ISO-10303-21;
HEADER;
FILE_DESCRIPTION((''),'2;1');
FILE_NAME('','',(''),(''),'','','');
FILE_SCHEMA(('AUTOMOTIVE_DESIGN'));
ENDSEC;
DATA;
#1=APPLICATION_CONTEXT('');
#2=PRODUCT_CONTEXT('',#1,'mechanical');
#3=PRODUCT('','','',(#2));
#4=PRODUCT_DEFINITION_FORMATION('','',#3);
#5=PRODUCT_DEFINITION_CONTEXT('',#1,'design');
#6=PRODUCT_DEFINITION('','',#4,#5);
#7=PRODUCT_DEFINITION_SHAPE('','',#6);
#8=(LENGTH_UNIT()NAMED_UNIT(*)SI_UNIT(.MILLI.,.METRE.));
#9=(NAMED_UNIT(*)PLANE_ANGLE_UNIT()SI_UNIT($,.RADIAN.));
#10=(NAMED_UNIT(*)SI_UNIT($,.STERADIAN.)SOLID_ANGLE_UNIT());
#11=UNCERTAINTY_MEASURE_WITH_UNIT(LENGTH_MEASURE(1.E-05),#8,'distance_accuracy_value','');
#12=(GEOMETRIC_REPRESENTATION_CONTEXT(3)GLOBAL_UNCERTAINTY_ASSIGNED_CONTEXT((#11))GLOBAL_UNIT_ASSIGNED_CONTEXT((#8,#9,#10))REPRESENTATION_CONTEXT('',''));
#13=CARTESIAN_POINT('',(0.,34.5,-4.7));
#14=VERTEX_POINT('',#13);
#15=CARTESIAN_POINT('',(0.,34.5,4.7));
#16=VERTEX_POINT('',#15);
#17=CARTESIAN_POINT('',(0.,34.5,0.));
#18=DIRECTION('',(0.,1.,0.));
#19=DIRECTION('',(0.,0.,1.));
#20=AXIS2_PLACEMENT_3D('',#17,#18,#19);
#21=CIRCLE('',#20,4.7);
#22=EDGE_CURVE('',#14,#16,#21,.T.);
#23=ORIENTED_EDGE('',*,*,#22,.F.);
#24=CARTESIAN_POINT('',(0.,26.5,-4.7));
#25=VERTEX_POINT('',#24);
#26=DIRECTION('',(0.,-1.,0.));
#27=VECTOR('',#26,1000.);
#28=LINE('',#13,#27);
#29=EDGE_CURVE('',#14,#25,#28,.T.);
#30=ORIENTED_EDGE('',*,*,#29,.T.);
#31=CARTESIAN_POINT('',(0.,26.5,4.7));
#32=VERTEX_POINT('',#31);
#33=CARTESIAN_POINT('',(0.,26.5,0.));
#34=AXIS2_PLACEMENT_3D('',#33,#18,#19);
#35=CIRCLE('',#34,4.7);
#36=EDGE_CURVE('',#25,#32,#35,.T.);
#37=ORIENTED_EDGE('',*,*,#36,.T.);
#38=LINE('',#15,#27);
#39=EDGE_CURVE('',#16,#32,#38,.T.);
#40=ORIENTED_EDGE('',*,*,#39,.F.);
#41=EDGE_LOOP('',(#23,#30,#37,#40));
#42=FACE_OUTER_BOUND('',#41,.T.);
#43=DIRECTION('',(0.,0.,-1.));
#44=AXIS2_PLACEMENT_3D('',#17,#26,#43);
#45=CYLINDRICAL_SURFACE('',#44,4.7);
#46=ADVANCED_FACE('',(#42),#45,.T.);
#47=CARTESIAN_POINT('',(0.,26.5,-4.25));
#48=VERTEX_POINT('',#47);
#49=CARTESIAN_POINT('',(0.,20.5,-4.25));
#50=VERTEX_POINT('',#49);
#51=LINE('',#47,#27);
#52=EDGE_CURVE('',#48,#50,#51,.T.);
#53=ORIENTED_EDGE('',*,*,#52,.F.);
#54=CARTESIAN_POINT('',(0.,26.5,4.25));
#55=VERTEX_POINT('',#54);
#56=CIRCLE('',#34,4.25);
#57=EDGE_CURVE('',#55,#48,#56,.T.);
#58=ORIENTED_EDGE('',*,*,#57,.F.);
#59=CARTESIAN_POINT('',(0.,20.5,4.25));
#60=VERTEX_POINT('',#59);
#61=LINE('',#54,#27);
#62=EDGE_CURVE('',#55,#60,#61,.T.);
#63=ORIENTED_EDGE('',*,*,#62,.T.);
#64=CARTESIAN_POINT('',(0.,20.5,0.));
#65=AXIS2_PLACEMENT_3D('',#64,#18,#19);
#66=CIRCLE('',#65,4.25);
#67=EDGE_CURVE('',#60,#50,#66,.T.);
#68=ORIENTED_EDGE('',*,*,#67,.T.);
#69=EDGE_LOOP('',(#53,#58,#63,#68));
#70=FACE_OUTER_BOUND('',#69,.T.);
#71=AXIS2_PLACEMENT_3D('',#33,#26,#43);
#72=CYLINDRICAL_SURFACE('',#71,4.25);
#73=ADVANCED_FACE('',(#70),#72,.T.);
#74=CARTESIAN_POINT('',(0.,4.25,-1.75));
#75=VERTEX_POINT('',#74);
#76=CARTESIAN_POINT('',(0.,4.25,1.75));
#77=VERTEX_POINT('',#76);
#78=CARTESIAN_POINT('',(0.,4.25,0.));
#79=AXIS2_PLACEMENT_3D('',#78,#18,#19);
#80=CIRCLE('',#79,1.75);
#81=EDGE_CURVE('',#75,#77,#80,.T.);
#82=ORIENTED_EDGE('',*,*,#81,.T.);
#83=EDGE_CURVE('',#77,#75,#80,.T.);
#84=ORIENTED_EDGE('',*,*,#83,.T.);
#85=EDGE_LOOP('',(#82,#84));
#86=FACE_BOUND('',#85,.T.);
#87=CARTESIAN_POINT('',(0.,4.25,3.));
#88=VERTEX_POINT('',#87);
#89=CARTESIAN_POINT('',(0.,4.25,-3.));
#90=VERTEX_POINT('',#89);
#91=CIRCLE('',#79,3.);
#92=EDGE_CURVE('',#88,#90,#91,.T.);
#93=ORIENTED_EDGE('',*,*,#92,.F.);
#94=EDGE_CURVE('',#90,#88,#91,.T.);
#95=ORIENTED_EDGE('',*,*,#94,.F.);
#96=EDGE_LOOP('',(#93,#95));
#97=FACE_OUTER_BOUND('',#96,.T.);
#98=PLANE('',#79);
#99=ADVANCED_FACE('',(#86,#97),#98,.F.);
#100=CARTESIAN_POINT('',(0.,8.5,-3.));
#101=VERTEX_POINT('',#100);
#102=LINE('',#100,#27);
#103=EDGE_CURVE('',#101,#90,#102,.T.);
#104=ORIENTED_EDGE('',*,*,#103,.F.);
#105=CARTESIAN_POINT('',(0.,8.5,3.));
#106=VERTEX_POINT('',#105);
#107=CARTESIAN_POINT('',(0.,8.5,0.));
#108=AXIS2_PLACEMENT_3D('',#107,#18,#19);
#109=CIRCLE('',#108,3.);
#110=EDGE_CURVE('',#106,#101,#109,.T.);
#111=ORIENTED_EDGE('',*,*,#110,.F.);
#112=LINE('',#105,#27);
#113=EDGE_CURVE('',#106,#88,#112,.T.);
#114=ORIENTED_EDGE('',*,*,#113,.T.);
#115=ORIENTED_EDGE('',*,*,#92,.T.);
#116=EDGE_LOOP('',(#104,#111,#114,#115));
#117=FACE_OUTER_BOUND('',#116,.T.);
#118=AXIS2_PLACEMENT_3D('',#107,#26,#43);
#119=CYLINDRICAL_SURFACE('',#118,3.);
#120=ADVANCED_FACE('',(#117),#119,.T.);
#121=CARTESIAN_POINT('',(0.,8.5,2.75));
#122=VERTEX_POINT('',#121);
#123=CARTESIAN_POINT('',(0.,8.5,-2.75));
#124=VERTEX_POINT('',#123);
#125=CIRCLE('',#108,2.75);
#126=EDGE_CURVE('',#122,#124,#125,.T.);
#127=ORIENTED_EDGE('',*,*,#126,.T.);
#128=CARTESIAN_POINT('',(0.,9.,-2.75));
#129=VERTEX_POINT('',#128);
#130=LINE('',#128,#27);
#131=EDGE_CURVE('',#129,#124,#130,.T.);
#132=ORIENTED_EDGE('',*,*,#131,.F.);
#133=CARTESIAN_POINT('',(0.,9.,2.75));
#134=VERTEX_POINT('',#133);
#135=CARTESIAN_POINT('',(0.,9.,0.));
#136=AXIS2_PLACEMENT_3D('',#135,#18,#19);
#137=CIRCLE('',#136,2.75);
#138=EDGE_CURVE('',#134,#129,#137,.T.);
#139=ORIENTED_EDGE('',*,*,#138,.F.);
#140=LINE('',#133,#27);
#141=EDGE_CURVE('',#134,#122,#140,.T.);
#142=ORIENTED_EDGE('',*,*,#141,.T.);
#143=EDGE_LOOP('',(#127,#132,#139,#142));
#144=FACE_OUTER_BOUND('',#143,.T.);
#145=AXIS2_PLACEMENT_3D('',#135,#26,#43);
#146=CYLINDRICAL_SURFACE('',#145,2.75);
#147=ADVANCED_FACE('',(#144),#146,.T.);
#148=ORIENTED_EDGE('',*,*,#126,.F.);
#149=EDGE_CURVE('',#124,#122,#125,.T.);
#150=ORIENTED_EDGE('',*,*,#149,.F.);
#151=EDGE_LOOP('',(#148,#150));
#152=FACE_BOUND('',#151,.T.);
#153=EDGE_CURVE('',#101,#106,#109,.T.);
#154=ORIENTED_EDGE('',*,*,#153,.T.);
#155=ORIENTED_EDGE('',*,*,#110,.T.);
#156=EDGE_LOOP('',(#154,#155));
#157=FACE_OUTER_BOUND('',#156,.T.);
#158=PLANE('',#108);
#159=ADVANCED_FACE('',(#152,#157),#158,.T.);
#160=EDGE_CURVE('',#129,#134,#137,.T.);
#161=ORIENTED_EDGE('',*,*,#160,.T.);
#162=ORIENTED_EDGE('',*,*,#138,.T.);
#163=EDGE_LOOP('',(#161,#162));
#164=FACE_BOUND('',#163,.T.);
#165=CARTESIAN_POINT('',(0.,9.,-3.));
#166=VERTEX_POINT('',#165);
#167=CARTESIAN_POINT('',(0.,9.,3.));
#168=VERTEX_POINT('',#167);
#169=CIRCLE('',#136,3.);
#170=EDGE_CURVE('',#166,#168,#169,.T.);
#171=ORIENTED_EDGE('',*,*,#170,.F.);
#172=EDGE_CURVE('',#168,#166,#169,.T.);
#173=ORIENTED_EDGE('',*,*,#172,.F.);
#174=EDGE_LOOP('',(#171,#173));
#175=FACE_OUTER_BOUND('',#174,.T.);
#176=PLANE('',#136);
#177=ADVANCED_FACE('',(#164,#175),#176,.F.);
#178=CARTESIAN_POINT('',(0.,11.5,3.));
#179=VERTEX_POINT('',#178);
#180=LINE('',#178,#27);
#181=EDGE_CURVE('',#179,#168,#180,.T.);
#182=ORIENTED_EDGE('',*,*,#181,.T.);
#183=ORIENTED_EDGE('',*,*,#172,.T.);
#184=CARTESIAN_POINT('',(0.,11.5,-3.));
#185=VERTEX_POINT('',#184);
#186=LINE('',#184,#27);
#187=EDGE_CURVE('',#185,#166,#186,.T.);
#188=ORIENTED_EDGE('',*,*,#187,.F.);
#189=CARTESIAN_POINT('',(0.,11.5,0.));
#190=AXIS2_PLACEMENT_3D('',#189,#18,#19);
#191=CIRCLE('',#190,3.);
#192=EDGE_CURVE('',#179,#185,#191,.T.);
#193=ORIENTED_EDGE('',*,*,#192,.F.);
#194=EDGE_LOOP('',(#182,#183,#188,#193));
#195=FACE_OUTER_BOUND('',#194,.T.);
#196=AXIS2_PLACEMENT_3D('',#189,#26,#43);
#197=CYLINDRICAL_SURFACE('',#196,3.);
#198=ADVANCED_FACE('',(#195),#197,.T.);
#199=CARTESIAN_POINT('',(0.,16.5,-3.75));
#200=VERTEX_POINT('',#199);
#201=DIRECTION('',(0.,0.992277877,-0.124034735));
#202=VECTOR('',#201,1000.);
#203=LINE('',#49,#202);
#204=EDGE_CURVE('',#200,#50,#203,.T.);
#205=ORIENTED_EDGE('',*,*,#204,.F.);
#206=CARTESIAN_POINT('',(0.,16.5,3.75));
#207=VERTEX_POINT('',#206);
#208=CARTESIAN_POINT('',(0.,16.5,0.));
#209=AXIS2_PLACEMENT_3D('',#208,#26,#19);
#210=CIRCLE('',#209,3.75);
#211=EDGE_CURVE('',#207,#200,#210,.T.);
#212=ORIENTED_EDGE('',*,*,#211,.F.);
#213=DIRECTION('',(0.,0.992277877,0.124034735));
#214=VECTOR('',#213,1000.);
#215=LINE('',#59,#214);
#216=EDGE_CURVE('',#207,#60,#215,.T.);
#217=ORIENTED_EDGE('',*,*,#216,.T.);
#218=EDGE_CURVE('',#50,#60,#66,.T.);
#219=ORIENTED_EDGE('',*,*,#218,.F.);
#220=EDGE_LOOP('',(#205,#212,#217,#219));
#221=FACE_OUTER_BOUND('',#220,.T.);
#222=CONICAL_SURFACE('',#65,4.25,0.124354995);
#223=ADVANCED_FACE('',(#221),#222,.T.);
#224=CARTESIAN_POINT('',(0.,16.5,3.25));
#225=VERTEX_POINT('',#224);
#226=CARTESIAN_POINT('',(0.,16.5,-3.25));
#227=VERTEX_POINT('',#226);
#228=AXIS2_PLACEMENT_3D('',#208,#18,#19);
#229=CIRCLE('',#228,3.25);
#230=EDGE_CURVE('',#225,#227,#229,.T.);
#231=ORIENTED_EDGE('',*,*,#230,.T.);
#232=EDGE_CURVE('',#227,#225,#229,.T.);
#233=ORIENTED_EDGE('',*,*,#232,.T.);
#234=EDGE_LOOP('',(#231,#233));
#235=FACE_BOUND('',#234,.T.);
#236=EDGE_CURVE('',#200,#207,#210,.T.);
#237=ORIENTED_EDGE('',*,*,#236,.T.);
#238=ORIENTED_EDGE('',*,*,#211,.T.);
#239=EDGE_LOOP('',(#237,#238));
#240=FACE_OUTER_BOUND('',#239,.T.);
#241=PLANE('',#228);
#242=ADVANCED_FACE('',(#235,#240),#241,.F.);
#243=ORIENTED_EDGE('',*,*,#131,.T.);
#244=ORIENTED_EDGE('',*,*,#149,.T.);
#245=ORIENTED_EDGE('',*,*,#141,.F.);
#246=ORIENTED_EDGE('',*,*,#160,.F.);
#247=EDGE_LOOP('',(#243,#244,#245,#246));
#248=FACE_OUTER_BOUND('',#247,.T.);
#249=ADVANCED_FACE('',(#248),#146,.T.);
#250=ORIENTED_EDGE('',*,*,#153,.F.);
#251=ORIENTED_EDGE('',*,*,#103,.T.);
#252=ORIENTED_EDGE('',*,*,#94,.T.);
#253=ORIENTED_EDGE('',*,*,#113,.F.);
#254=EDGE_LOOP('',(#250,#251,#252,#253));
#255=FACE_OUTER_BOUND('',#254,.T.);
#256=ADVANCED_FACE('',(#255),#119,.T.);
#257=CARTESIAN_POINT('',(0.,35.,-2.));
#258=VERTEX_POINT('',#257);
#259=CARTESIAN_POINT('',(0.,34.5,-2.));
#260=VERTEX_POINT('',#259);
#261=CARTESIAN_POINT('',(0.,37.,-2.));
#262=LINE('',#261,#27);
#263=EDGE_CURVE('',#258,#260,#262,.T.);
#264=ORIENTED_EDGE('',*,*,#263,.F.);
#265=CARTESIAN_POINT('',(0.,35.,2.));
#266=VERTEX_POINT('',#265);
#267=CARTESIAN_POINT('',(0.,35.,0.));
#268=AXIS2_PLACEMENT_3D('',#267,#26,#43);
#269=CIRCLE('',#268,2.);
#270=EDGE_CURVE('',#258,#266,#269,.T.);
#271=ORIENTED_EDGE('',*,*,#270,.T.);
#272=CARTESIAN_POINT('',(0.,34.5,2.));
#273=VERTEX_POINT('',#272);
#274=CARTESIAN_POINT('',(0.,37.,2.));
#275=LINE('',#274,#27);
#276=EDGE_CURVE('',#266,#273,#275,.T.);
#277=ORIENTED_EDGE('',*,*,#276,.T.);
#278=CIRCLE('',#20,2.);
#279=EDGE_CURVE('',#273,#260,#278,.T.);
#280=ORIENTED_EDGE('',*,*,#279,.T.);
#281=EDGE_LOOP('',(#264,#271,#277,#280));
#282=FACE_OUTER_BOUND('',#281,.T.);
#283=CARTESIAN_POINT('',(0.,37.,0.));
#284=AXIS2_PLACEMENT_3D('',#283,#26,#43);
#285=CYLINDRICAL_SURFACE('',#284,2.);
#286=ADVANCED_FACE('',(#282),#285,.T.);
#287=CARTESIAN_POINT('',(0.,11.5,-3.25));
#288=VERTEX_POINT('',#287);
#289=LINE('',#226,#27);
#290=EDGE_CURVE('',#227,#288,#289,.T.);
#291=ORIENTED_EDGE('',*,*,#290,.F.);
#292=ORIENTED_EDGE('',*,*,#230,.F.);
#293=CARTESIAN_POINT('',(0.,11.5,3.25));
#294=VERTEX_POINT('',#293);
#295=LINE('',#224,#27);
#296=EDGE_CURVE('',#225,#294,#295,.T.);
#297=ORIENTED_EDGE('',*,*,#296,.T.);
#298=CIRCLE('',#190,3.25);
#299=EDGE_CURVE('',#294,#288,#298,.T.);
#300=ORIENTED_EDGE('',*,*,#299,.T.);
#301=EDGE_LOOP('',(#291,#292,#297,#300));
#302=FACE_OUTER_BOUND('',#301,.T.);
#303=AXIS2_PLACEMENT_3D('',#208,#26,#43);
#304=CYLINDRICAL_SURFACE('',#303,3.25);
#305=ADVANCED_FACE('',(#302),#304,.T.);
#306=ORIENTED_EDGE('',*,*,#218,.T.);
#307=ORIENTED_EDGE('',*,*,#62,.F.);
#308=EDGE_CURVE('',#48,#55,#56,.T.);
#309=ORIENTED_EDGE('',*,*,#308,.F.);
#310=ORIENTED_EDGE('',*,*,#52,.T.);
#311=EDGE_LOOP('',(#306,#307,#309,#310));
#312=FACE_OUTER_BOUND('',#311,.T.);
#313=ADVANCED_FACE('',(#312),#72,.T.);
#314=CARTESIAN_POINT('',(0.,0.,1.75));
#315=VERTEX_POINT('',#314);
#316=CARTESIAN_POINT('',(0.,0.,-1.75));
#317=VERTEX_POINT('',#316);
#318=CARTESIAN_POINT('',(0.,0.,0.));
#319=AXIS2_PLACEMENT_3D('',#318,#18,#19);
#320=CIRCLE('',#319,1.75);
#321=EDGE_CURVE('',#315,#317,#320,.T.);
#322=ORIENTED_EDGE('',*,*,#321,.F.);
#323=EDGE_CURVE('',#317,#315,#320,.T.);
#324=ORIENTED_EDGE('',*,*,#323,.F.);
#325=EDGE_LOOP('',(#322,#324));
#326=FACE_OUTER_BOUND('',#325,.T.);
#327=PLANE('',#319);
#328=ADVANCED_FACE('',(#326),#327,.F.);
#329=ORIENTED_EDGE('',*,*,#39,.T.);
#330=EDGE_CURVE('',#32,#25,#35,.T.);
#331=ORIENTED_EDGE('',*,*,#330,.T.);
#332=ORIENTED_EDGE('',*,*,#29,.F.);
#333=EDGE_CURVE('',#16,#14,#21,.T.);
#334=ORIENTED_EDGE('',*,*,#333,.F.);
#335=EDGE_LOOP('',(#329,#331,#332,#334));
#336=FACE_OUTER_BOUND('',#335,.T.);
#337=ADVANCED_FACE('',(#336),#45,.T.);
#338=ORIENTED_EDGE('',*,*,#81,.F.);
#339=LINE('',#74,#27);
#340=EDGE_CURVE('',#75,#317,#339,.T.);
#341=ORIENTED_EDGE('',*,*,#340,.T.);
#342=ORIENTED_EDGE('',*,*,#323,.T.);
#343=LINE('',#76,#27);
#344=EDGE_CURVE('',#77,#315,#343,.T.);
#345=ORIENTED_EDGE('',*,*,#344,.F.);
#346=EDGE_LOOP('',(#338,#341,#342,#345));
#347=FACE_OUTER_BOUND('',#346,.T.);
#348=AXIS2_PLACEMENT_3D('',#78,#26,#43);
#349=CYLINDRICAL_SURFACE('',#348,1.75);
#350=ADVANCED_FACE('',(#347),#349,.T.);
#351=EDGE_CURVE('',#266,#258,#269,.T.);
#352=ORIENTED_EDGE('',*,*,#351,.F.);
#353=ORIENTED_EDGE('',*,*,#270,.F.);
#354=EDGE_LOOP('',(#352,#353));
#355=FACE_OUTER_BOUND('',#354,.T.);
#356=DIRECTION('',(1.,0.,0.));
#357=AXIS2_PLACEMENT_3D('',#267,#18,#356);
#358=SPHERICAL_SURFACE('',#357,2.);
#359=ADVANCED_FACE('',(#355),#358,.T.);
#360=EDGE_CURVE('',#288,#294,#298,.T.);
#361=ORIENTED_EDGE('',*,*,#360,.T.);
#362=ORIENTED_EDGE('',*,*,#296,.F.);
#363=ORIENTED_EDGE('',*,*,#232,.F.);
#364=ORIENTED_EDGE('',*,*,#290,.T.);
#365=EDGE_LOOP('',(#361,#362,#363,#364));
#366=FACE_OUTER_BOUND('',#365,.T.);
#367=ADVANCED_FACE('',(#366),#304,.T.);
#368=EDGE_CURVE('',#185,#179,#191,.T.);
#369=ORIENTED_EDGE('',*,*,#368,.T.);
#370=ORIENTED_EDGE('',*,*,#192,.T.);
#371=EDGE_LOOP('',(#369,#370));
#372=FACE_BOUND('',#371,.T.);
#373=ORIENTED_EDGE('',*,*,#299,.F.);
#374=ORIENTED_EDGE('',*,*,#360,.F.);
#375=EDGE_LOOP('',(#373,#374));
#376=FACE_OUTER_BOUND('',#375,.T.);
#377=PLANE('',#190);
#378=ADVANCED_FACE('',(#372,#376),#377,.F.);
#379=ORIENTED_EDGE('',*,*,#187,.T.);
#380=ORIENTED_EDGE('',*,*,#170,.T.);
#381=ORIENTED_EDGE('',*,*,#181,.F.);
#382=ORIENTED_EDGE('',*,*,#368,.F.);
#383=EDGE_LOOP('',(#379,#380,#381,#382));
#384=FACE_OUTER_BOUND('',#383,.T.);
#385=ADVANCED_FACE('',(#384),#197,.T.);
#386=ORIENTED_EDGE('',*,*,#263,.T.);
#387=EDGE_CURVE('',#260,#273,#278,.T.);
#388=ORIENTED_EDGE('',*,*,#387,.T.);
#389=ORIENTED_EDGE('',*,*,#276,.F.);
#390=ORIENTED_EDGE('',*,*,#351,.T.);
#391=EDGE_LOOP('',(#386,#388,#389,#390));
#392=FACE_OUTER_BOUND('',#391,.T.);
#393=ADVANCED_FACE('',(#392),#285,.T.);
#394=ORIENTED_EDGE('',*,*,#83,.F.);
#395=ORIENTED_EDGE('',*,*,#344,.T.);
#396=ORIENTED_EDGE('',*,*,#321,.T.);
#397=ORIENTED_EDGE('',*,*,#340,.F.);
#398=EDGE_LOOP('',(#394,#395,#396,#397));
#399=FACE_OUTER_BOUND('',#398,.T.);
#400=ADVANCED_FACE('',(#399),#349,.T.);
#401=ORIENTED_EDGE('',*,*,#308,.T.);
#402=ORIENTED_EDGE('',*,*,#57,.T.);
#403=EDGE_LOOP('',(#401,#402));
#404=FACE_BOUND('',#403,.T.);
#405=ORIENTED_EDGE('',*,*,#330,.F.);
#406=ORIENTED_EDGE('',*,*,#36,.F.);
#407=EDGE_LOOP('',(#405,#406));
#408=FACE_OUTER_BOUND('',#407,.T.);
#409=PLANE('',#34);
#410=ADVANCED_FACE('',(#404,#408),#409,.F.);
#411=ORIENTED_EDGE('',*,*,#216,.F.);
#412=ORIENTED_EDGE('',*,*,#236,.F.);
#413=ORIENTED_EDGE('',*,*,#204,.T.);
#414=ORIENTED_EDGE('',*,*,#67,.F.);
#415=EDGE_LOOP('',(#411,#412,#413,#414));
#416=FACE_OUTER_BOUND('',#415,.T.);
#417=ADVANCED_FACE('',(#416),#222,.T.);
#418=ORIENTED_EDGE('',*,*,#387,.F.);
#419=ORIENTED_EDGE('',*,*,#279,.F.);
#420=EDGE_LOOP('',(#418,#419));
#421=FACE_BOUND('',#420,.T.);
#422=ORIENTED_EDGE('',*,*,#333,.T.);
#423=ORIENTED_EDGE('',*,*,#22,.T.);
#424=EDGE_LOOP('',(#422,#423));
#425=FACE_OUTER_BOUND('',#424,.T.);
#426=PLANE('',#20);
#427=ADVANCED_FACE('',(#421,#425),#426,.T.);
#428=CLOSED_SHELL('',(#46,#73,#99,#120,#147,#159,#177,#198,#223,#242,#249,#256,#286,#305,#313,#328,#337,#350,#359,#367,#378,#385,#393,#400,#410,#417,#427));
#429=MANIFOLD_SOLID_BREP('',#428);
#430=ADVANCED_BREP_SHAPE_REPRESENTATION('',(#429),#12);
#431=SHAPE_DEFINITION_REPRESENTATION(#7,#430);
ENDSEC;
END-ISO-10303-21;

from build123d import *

# Parameters (mm, degrees)
SKETCH1_R           = 1.75
BOSS_EXTRUDE1_DEPTH = 4.25
SKETCH2_R           = 3
BOSS_EXTRUDE2_DEPTH = 4.25
SKETCH3_R           = 2.75
BOSS_EXTRUDE3_DEPTH = 0.5
SKETCH4_R           = 3
BOSS_EXTRUDE4_DEPTH = 2.5
SKETCH5_R           = 3.25
BOSS_EXTRUDE5_DEPTH = 5
SKETCH6_R           = 4.25
BOSS_EXTRUDE6_DEPTH = 10
CHAMFER1_SIZE       = 0.5
CHAMFER1_SIZE2      = 4
SKETCH7_R           = 4.7
BOSS_EXTRUDE7_DEPTH = 8
SKETCH8_R           = 2
BOSS_EXTRUDE8_DEPTH = 2.5
FILLET1_R           = 2


with BuildPart() as part:
    # Sketch1 → Boss-Extrude1 (new body)
    with BuildSketch(Plane(origin=(0, 0, 0), x_dir=(1, 0, 0), z_dir=(0, 1, 0))):
        with Locations(Location((0, 0, 0), (0, 0, 270))):
            Circle(SKETCH1_R)
    extrude(amount=BOSS_EXTRUDE1_DEPTH)

    # Sketch2 → Boss-Extrude2 (add)
    with BuildSketch(Plane(origin=(0, 4.25, 0), x_dir=(1, 0, 0), z_dir=(0, 1, 0))):
        with Locations(Location((0, 0, 0), (0, 0, 270))):
            Circle(SKETCH2_R)
    extrude(amount=BOSS_EXTRUDE2_DEPTH)

    # Sketch3 → Boss-Extrude3 (add)
    with BuildSketch(Plane(origin=(0, 8.5, 0), x_dir=(1, 0, 0), z_dir=(0, 1, 0))):
        with Locations(Location((0, 0, 0), (0, 0, 270))):
            Circle(SKETCH3_R)
    extrude(amount=BOSS_EXTRUDE3_DEPTH)

    # Sketch4 → Boss-Extrude4 (add)
    with BuildSketch(Plane(origin=(0, 9, 0), x_dir=(1, 0, 0), z_dir=(0, 1, 0))):
        with Locations(Location((0, 0, 0), (0, 0, 270))):
            Circle(SKETCH4_R)
    extrude(amount=BOSS_EXTRUDE4_DEPTH)

    # Sketch5 → Boss-Extrude5 (add)
    with BuildSketch(Plane(origin=(0, 11.5, 0), x_dir=(1, 0, 0), z_dir=(0, 1, 0))):
        with Locations(Location((0, 0, 0), (0, 0, 270))):
            Circle(SKETCH5_R)
    extrude(amount=BOSS_EXTRUDE5_DEPTH)

    # Sketch6 → Boss-Extrude6 (add)
    with BuildSketch(Plane(origin=(0, 16.5, 0), x_dir=(1, 0, 0), z_dir=(0, 1, 0))):
        with Locations(Location((0, 0, 0), (0, 0, 270))):
            Circle(SKETCH6_R)
    extrude(amount=BOSS_EXTRUDE6_DEPTH)

    # Chamfer1
    chamfer1_edges = [part.edges().sort_by_distance(p)[0] for p in [
        (0, 16.5, -4.25),
    ]]
    chamfer1_side = [part.faces().sort_by_distance(p)[0] for p in [
        (0, 16.5, -4.129791847),
    ]]
    chamfer(chamfer1_edges, length=CHAMFER1_SIZE, length2=CHAMFER1_SIZE2, reference=chamfer1_side[0])

    # Sketch7 → Boss-Extrude7 (add)
    with BuildSketch(Plane(origin=(0, 26.5, 0), x_dir=(1, 0, 0), z_dir=(0, 1, 0))):
        with Locations(Location((0, 0, 0), (0, 0, 270))):
            Circle(SKETCH7_R)
    extrude(amount=BOSS_EXTRUDE7_DEPTH)

    # Sketch8 → Boss-Extrude8 (add)
    with BuildSketch(Plane(origin=(0, 34.5, 0), x_dir=(1, 0, 0), z_dir=(0, 1, 0))):
        with Locations(Location((0, 0, 0), (0, 0, 270))):
            Circle(SKETCH8_R)
    extrude(amount=BOSS_EXTRUDE8_DEPTH)

    # Fillet1
    fillet1_edges = [part.edges().sort_by_distance(p)[0] for p in [
        (0, 37, -2),
    ]]
    fillet(fillet1_edges, radius=FILLET1_R)


solid = part.part
